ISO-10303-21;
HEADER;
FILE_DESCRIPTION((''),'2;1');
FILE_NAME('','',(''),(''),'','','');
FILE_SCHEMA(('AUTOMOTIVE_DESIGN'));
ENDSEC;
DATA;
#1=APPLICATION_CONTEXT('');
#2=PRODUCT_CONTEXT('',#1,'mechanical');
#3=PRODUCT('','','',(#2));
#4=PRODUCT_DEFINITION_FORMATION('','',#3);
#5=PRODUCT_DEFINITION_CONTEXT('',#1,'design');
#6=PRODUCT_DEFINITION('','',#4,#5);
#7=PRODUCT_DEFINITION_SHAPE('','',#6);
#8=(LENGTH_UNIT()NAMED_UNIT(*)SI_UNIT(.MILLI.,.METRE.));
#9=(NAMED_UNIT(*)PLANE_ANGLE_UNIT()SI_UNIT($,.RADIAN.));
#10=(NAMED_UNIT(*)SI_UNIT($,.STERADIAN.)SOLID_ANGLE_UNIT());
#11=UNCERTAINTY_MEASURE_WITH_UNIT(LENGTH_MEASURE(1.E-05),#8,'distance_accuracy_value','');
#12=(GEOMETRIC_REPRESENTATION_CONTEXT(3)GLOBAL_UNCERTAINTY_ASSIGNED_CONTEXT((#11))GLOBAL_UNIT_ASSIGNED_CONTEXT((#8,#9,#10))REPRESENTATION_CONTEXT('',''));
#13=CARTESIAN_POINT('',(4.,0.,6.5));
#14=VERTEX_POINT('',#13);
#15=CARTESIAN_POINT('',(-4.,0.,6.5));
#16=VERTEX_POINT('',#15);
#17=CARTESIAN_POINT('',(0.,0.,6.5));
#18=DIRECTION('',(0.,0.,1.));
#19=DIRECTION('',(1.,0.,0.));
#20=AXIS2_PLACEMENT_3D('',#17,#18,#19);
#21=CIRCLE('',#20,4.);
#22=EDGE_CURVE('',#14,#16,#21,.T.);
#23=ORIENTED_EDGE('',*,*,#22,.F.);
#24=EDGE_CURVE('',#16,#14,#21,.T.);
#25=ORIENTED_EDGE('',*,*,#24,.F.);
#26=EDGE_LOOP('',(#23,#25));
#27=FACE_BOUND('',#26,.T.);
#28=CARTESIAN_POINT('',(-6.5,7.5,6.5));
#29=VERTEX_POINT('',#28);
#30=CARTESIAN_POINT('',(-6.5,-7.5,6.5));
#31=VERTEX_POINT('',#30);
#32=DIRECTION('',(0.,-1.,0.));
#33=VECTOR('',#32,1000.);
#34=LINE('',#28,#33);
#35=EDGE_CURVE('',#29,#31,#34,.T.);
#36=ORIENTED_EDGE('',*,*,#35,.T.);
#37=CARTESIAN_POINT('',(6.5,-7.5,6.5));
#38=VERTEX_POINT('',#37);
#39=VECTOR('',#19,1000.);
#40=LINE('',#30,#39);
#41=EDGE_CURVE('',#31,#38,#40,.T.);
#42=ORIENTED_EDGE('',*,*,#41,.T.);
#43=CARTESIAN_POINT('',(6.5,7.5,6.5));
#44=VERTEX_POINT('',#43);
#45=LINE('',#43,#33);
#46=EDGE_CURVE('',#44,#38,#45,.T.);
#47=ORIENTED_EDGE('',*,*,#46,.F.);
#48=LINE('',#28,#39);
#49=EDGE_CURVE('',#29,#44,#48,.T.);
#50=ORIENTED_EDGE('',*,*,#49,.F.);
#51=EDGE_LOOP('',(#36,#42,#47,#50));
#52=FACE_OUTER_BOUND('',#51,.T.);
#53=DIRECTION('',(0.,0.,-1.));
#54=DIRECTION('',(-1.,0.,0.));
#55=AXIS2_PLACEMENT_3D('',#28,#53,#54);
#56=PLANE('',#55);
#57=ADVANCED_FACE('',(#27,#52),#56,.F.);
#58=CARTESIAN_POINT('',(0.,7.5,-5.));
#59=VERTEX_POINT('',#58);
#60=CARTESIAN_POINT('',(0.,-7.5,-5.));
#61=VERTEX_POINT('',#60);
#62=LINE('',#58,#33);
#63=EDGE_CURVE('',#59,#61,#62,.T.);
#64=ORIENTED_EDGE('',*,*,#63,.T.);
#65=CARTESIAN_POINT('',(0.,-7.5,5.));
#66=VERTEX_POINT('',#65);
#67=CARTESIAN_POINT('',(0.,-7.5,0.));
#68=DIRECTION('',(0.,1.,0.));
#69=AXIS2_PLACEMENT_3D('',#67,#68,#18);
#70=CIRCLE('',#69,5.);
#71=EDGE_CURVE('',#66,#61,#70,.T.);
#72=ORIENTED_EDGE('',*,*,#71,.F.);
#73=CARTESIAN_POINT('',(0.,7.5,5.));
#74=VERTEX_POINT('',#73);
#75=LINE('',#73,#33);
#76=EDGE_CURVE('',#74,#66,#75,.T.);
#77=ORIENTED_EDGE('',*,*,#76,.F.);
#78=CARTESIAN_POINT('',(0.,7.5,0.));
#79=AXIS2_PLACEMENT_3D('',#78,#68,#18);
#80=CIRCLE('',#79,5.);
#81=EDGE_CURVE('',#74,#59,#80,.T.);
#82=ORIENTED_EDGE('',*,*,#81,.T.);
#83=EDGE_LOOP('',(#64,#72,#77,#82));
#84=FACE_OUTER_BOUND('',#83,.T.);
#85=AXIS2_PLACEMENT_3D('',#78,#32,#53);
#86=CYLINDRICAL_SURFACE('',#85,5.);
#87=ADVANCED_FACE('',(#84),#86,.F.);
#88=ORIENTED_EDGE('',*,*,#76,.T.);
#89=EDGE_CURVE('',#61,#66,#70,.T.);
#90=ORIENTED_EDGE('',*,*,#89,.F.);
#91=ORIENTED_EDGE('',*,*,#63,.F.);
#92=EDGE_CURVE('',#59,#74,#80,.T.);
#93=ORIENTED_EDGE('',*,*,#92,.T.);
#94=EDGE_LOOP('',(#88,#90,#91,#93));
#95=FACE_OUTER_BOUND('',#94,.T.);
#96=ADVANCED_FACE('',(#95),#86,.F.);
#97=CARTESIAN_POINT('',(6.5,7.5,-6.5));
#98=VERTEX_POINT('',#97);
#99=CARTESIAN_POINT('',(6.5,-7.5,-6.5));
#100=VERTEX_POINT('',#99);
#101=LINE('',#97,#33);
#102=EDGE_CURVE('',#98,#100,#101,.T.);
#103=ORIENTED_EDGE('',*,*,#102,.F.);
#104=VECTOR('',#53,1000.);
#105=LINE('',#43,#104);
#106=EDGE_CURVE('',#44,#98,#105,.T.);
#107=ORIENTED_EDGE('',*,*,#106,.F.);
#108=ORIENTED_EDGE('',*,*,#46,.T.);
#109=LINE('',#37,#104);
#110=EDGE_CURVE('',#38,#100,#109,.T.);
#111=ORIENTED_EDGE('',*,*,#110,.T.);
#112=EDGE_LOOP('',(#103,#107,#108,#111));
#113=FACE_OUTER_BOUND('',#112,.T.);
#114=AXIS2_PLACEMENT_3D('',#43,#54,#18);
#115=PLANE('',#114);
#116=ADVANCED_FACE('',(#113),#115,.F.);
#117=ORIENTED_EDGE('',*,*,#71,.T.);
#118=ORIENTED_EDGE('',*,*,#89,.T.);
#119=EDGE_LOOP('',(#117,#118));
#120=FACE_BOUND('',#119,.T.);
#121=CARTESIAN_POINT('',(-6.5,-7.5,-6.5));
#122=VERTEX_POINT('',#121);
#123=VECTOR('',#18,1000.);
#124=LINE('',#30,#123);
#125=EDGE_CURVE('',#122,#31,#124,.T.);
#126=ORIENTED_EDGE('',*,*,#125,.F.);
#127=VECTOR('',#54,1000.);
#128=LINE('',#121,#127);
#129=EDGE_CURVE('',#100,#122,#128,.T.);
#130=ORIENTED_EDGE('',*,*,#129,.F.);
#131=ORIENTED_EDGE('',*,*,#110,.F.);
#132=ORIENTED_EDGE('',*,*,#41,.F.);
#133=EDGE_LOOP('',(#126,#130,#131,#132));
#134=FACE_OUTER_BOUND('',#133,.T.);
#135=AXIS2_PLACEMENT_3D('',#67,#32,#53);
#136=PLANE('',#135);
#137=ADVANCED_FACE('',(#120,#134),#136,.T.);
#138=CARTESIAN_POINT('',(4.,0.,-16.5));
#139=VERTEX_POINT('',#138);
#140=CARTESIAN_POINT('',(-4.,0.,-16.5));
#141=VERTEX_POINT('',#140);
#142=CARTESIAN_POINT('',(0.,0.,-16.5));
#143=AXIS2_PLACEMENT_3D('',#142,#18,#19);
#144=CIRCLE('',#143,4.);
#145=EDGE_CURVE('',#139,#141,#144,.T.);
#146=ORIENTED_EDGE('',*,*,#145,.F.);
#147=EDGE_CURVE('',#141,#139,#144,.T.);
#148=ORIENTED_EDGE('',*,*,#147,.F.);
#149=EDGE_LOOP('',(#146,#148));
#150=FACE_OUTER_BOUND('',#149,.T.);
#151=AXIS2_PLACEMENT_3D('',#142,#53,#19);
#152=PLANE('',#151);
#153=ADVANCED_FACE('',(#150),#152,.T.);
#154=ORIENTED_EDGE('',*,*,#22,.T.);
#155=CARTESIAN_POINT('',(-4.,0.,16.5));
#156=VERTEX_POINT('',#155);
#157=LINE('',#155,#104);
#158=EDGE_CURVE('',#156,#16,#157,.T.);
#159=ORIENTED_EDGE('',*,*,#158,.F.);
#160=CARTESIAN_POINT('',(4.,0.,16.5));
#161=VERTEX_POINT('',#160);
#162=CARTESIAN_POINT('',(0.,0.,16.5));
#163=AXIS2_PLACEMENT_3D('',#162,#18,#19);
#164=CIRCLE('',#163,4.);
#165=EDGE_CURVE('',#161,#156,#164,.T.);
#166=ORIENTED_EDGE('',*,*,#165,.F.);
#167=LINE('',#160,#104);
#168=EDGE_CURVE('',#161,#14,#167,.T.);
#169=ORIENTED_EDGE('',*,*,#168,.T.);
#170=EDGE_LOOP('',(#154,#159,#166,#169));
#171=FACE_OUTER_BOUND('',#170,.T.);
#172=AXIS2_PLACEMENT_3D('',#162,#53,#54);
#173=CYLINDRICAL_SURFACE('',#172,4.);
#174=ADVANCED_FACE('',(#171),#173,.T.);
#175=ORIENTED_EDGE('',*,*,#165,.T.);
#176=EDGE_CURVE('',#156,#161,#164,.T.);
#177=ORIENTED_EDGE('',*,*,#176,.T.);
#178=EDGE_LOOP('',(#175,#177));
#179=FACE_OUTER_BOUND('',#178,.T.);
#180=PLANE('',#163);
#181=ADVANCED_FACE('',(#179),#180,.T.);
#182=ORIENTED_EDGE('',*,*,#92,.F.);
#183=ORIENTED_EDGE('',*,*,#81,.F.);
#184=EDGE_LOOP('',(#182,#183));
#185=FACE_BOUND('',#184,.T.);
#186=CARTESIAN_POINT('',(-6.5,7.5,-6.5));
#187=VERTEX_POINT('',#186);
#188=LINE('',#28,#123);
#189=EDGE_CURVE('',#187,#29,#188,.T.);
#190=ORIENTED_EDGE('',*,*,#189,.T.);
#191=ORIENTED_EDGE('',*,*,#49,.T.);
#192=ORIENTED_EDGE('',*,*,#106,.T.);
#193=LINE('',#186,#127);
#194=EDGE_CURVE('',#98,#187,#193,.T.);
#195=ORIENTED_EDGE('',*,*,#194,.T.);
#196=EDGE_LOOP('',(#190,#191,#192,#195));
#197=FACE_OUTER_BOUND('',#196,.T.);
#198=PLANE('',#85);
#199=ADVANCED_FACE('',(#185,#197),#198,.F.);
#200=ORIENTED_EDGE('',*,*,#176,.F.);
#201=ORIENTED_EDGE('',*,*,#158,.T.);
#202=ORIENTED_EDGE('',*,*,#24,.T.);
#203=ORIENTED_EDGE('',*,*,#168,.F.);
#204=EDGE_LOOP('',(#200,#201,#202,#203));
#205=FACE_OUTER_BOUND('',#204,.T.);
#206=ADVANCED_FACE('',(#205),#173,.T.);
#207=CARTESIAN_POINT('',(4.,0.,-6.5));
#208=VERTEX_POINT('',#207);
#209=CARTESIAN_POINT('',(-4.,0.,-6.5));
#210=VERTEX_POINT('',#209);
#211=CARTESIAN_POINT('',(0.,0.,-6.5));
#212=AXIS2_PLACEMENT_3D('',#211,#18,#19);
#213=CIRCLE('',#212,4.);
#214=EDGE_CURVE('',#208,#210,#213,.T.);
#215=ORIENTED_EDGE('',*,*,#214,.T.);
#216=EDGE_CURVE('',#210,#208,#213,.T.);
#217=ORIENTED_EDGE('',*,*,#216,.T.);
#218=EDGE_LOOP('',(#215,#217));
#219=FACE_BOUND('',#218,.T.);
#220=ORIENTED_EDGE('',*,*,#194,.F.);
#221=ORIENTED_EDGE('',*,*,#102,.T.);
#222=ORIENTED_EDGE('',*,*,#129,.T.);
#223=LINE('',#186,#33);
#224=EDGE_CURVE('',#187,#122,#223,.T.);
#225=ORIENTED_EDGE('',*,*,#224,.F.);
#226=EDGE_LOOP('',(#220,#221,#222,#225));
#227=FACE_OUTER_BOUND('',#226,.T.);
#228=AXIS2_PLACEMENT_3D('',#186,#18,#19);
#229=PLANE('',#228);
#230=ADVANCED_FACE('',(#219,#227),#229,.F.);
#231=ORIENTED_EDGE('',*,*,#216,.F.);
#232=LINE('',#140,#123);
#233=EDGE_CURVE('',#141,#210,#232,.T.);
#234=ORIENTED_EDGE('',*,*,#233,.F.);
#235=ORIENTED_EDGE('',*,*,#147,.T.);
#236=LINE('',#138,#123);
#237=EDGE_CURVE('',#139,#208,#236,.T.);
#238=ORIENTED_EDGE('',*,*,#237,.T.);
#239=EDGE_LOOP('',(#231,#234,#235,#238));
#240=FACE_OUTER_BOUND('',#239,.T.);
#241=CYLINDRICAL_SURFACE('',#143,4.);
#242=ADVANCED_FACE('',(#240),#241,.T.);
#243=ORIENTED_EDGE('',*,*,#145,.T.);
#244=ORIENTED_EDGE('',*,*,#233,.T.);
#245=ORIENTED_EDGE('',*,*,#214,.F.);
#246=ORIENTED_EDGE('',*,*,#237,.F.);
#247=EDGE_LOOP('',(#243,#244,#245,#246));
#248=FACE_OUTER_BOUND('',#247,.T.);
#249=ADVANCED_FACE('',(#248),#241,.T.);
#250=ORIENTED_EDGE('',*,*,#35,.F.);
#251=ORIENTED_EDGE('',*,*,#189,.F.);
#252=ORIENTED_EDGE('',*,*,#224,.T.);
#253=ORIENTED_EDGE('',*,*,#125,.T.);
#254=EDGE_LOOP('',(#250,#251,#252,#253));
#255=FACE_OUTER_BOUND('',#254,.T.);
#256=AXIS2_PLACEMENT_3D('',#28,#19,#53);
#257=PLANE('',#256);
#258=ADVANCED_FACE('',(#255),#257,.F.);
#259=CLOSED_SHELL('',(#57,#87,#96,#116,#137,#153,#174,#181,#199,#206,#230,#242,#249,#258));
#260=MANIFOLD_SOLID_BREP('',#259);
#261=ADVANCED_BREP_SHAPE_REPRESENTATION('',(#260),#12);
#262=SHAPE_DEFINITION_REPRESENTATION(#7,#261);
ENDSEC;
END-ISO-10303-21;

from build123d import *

# Parameters (mm, degrees)
SKETCH1_W           = 13
SKETCH1_H           = 13
SKETCH1_R           = 5
BOSS_EXTRUDE1_DEPTH = 7.5
SKETCH2_R           = 4
BOSS_EXTRUDE2_DEPTH = 10


with BuildPart() as part:
    # Sketch1 → Boss-Extrude1 (new, symmetric)
    with BuildSketch(Plane(origin=(0, 0, 0), x_dir=(1, 0, 0), z_dir=(0, 1, 0))):
        Rectangle(SKETCH1_W, SKETCH1_H)
        with Locations(Location((0, 0, 0), (0, 0, 270))):
            Circle(SKETCH1_R, mode=Mode.SUBTRACT)
    extrude(amount=BOSS_EXTRUDE1_DEPTH, both=True)

    # Sketch2 → Boss-Extrude2 (add)
    with BuildSketch(Plane.XY.offset(6.5)):
        Circle(SKETCH2_R)
    boss_extrude2 = extrude(amount=BOSS_EXTRUDE2_DEPTH)

    # Mirror1: Boss-Extrude2 across plane
    add(boss_extrude2.mirror(Plane.XY))


solid = part.part
